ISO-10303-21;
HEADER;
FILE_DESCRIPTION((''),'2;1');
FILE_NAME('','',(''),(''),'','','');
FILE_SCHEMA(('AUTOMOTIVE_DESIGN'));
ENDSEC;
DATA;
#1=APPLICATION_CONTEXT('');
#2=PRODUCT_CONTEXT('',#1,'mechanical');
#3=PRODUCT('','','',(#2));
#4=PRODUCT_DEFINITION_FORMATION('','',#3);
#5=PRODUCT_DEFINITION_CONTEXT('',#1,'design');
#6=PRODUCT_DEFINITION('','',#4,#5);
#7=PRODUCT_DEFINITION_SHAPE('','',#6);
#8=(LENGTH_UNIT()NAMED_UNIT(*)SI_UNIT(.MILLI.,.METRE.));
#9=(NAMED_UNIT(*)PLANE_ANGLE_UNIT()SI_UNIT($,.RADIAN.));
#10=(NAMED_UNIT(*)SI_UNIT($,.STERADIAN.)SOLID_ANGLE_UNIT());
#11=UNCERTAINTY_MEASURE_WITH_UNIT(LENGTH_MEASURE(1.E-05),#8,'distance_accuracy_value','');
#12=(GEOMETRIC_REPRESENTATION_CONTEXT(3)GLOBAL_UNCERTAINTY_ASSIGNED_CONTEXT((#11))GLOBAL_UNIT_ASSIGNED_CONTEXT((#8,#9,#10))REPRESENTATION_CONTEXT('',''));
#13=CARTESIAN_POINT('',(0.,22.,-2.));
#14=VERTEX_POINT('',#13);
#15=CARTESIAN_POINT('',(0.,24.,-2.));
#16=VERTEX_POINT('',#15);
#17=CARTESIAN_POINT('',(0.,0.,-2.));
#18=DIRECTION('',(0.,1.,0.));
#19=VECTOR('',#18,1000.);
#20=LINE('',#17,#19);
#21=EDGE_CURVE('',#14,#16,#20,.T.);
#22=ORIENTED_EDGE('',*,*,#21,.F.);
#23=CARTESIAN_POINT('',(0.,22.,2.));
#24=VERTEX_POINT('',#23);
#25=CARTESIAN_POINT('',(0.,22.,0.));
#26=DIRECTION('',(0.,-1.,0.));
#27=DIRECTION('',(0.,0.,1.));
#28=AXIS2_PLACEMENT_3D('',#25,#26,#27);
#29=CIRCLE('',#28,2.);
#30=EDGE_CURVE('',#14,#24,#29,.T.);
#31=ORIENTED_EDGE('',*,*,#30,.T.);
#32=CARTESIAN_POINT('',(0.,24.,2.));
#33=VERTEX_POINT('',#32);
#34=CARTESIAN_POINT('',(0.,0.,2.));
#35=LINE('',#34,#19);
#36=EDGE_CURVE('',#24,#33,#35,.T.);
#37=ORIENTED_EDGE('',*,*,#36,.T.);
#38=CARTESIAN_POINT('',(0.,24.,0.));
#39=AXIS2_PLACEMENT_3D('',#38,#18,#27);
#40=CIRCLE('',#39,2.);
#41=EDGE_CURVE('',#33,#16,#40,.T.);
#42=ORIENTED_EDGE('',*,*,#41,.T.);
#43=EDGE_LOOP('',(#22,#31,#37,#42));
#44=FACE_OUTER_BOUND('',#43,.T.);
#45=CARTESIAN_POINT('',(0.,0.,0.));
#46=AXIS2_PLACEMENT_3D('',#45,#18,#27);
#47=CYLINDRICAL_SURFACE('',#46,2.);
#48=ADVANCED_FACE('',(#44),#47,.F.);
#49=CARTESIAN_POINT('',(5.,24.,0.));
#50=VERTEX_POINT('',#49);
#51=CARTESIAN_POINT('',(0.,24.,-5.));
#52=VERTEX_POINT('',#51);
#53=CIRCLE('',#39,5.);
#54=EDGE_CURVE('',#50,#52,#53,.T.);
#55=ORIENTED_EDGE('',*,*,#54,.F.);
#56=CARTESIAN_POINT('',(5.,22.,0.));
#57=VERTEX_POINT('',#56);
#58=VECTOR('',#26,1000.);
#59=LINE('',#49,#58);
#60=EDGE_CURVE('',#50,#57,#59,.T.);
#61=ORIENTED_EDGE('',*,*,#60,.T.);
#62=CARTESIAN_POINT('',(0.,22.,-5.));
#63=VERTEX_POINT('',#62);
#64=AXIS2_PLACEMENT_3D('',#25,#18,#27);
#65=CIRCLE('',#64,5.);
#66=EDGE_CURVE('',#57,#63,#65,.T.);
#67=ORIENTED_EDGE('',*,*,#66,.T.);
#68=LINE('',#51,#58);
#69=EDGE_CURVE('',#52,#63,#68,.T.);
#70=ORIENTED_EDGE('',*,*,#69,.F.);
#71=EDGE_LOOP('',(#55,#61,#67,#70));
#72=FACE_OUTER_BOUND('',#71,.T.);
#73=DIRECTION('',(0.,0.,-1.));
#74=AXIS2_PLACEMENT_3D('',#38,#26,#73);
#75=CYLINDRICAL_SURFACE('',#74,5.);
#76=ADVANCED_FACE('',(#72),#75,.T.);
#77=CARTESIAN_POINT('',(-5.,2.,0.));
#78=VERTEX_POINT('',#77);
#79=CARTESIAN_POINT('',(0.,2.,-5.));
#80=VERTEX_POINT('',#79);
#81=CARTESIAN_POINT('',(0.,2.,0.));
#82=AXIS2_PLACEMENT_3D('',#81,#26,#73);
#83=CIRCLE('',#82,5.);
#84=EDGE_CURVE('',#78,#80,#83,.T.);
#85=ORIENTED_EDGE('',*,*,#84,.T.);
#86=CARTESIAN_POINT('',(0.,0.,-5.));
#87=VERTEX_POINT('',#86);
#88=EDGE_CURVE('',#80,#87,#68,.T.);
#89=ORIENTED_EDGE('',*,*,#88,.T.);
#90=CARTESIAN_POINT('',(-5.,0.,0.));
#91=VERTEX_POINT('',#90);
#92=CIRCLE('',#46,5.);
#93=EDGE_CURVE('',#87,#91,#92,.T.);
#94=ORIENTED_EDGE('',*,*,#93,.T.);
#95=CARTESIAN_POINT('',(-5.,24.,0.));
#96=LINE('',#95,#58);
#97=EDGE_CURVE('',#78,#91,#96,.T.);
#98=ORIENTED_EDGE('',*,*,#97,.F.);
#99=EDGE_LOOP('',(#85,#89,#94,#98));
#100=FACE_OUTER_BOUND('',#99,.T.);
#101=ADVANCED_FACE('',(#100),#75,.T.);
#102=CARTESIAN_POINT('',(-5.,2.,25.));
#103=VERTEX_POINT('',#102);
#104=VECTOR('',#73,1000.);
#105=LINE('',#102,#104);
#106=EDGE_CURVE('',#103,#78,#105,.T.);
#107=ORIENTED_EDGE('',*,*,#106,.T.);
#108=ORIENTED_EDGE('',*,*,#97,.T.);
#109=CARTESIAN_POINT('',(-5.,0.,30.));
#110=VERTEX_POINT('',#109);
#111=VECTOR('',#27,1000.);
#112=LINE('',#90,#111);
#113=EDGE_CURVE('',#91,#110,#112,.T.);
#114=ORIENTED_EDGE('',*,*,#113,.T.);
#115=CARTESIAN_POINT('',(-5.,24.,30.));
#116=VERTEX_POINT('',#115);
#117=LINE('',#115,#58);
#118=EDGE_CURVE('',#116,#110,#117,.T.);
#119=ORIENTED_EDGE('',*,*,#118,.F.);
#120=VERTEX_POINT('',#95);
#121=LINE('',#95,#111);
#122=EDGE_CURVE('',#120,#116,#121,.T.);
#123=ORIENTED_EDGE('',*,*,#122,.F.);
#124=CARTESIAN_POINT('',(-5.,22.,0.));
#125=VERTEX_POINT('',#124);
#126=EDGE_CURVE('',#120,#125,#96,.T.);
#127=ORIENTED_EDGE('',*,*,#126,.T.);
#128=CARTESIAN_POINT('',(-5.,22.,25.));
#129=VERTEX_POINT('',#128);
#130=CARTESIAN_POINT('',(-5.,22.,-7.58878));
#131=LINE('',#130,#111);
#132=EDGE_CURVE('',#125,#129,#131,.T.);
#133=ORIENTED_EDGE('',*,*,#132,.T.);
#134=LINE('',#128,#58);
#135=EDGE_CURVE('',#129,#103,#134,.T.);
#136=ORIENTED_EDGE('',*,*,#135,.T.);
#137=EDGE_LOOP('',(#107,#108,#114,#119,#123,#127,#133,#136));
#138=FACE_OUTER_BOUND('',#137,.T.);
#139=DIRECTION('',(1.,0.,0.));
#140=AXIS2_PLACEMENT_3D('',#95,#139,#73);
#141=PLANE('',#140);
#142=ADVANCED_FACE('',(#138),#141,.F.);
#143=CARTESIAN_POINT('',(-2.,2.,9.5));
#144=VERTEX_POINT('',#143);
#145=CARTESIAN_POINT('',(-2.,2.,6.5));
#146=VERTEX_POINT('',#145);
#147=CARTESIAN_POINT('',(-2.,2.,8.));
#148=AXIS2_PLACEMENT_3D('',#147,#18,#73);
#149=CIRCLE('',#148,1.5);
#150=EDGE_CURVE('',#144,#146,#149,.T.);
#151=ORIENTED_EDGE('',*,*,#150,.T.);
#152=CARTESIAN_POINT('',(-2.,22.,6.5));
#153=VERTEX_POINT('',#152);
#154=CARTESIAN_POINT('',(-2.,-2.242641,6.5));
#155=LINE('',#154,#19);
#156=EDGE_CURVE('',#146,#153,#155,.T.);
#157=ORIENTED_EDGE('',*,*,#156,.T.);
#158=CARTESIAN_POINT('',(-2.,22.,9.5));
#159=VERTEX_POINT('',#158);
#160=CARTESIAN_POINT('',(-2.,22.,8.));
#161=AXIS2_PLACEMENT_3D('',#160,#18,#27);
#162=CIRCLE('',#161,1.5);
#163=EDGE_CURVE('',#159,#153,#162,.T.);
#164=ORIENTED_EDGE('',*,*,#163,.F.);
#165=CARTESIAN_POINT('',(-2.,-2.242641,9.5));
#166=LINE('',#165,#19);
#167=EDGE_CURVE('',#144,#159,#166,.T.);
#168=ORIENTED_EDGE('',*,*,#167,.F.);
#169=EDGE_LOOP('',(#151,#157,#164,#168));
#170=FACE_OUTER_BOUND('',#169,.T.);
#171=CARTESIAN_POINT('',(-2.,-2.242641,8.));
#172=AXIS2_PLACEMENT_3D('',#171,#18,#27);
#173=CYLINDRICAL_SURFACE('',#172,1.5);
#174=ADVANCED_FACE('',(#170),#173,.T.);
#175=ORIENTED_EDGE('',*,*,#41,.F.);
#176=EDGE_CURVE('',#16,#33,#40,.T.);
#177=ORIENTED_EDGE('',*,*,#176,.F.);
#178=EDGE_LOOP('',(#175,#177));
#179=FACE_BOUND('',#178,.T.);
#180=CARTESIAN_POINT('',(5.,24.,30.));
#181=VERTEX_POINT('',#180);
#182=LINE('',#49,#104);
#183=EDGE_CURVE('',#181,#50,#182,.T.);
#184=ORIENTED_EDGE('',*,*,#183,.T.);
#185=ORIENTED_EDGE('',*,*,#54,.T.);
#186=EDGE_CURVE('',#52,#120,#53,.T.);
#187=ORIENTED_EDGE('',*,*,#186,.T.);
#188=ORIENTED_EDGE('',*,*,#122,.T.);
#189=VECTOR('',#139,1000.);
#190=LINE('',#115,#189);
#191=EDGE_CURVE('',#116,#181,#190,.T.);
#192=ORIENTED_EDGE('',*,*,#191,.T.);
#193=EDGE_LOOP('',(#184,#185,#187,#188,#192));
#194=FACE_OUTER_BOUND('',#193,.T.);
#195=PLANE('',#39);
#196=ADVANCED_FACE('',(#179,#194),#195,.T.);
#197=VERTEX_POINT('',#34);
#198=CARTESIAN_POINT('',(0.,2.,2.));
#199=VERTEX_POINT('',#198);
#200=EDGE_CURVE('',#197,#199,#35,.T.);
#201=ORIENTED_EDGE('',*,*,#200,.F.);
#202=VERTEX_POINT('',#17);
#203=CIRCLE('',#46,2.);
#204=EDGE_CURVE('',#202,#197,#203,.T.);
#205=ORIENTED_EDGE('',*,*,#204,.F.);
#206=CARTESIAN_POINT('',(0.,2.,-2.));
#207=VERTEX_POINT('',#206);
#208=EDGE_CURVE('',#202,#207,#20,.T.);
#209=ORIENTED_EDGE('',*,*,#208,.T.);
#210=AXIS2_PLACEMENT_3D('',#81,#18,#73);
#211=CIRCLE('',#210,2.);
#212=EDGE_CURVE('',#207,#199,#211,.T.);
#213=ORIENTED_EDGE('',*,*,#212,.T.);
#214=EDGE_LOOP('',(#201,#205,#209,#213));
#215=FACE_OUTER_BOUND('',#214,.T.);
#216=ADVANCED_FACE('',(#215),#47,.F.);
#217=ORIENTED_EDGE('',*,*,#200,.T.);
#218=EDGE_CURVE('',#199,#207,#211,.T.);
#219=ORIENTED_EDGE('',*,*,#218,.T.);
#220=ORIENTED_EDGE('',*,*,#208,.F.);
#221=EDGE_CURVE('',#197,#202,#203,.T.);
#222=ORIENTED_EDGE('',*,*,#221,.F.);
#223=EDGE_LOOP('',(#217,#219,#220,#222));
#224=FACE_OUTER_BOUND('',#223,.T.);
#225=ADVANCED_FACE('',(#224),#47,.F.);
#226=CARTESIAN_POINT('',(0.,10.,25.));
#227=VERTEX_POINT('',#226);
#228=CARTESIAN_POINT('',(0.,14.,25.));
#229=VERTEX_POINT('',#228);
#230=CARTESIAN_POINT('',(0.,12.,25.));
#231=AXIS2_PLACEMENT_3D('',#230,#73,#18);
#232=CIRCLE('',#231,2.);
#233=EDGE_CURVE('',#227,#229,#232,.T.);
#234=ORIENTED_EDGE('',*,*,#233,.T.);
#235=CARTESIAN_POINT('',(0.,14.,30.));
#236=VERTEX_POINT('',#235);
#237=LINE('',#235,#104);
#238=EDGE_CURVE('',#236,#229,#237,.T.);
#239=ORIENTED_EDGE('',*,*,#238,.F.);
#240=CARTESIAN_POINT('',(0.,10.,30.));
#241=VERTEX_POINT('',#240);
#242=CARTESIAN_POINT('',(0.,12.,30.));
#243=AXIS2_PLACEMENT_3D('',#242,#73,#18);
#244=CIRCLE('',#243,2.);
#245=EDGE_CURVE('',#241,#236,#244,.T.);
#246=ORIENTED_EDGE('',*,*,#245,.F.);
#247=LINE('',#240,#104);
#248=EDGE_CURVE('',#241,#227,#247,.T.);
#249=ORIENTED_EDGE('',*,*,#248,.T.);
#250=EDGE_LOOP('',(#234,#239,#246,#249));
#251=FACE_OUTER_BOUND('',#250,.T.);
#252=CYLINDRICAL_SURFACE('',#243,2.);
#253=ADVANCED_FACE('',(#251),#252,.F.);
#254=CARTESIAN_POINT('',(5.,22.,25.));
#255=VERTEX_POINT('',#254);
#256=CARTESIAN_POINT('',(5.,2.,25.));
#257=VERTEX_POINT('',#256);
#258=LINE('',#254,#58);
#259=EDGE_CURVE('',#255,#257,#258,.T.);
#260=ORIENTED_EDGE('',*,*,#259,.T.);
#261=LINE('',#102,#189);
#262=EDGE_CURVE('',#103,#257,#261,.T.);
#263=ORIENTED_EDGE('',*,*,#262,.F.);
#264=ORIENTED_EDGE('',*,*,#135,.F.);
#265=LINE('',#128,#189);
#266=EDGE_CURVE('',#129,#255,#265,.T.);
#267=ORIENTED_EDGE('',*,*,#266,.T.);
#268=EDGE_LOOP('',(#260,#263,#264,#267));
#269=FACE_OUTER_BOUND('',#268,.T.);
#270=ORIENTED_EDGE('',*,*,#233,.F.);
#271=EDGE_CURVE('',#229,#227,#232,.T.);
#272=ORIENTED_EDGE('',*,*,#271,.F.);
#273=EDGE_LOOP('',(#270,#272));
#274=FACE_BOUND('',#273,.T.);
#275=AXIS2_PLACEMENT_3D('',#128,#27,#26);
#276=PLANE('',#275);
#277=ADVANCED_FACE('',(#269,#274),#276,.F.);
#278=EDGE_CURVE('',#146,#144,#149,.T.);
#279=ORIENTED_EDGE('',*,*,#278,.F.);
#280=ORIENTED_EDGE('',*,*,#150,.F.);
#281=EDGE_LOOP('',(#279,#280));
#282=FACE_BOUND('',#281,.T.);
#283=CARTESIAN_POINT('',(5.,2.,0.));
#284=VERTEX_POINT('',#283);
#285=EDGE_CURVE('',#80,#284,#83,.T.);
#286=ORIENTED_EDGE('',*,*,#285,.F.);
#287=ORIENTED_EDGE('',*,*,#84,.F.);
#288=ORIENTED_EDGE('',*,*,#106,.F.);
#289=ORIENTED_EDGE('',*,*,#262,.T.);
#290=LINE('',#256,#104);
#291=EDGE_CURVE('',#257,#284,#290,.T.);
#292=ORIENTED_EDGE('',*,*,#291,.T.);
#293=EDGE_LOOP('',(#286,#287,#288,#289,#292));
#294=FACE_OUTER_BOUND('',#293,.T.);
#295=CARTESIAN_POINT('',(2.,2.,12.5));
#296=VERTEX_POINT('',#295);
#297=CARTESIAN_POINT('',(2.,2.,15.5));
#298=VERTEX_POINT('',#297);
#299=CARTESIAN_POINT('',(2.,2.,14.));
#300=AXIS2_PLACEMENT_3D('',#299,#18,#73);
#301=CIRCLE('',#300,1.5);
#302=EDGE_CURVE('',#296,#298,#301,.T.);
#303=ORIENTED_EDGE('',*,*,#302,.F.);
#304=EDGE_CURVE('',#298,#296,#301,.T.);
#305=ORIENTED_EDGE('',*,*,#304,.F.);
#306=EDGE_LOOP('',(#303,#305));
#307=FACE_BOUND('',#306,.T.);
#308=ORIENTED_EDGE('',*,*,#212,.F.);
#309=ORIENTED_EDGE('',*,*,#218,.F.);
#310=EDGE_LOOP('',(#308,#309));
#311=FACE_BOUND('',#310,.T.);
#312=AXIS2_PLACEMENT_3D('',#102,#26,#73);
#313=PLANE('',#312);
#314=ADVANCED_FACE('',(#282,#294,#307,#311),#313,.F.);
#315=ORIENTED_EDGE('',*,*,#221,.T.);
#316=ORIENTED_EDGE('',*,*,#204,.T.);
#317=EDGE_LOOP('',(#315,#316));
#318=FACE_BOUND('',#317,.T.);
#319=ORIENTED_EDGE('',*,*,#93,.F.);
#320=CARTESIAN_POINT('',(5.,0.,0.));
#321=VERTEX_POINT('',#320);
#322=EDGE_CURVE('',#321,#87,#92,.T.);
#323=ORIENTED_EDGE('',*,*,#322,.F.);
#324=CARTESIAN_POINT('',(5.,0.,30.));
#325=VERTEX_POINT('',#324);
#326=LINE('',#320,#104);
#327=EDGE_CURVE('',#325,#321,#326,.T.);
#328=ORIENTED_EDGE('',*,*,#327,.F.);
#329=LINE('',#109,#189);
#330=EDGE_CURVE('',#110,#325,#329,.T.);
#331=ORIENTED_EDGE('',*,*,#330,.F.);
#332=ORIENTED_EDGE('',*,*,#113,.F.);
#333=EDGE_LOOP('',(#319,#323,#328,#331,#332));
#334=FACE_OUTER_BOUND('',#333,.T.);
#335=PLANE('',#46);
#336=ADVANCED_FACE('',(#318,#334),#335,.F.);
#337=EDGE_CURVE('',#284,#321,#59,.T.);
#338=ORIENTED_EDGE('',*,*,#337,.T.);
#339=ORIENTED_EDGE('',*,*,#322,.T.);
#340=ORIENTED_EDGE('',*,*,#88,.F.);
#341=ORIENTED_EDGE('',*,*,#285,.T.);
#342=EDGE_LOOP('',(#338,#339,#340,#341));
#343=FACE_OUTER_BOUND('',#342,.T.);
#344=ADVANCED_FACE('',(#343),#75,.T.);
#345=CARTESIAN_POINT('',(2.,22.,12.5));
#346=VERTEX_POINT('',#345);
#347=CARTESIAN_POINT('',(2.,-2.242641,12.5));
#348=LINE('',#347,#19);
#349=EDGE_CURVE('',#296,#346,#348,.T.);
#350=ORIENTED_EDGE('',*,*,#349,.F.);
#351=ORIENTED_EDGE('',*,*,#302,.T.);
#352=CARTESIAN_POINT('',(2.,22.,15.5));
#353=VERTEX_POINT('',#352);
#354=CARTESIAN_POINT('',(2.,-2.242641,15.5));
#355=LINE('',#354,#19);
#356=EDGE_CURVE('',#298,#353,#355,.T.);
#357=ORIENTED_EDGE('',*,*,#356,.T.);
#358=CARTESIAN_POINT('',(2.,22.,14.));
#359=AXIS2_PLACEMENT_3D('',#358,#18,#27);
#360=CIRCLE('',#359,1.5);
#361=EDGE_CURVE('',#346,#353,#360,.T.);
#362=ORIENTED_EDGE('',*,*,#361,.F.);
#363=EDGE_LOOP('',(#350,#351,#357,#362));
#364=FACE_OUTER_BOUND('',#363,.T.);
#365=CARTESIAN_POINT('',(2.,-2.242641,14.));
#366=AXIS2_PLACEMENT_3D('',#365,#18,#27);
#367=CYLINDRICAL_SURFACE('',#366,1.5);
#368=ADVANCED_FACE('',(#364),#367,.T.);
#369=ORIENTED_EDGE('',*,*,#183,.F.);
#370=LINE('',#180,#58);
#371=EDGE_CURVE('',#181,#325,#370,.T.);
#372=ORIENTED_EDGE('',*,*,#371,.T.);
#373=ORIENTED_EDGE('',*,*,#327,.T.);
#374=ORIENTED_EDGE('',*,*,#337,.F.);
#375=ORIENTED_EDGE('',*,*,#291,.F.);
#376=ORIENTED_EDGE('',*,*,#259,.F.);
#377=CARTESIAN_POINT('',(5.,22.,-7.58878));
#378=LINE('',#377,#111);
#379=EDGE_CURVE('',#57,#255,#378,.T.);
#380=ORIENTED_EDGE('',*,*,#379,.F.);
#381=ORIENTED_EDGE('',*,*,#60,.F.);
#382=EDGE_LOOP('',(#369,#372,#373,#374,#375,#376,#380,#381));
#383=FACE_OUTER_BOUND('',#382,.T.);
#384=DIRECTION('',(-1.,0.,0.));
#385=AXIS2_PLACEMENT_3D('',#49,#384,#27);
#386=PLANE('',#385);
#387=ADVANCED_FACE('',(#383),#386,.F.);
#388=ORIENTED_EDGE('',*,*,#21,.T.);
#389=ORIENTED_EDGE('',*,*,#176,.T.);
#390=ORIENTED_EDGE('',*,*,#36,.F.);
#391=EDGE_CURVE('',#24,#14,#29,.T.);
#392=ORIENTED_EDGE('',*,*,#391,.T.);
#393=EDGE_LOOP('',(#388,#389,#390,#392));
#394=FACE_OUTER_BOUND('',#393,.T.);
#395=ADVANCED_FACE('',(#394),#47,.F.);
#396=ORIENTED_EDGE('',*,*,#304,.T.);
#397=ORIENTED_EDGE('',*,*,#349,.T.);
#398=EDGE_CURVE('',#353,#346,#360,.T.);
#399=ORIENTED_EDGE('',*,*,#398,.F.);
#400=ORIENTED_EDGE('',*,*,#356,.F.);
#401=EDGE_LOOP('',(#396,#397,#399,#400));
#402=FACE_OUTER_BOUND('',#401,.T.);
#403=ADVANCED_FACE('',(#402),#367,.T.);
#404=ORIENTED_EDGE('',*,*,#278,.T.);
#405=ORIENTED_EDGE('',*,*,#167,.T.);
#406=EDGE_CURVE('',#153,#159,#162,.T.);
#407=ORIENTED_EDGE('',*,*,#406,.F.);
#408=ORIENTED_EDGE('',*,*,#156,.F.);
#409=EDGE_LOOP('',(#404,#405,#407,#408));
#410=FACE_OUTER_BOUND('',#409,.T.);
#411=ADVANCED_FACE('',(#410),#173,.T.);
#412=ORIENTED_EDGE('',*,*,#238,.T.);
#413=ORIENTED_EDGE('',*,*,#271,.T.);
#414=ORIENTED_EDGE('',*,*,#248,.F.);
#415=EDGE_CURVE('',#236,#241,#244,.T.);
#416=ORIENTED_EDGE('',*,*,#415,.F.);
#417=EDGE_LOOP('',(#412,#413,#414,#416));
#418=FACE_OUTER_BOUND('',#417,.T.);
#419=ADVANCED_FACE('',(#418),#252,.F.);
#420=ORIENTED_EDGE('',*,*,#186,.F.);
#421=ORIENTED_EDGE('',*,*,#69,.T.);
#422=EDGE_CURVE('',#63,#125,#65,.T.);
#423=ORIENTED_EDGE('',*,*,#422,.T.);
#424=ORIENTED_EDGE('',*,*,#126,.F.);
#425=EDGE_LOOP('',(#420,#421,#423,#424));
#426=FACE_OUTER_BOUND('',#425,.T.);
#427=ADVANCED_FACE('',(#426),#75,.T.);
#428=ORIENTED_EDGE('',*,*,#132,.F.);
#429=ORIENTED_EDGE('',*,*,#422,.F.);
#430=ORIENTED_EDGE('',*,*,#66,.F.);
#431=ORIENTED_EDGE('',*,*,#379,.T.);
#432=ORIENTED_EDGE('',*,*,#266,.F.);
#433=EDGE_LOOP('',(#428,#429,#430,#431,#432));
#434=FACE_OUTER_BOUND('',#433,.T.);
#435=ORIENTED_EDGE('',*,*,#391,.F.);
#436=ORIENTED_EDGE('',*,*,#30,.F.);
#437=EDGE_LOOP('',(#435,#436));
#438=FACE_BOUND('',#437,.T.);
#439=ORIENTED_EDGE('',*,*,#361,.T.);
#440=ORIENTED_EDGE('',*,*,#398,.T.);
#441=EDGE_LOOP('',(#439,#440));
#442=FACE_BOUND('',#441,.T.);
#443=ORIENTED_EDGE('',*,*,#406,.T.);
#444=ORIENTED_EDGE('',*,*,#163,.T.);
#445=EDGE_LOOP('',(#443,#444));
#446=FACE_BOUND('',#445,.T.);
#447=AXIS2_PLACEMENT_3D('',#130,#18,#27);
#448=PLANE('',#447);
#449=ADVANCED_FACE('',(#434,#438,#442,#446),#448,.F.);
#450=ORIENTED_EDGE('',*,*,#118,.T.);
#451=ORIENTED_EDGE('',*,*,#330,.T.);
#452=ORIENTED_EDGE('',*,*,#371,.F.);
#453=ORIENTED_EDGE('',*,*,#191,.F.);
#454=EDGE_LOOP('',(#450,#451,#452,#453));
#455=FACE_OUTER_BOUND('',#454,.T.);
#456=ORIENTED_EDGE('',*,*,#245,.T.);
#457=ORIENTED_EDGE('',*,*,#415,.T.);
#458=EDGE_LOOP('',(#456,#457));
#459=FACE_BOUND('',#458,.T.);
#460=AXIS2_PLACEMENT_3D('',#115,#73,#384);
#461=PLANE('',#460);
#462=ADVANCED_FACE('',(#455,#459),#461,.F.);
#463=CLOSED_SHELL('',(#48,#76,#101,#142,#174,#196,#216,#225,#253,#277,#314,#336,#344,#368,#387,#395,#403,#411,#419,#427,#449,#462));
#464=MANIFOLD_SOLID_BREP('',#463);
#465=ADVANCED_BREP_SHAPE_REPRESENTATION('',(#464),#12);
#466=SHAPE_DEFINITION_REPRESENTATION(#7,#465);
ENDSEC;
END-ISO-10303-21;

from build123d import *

# Parameters (mm, degrees)
BOSS_EXTRUDE1_DEPTH     = 24
CUT_EXTRUDE2_DEPTH      = 39.742741256
CUT_EXTRUDE2_DEPTH_BACK = 39.742741256
SKETCH4_R               = 2
CUT_EXTRUDE3_DEPTH      = 39.742741256
CUT_EXTRUDE3_DEPTH_BACK = 39.742741256
SKETCH6_W               = 32.588779774
SKETCH6_H               = 20
SKETCH7_R               = 2
CUT_EXTRUDE4_DEPTH      = 39.742741256
SKETCH8_R               = 1.5
BOSS_EXTRUDE3_DEPTH     = 22


with BuildPart() as part:
    # Sketch1 → Boss-Extrude1 (new body)
    with BuildSketch(Plane(origin=(0, 0, 0), x_dir=(1, 0, 0), z_dir=(0, 1, 0))):
        with BuildLine():
            Line((-5, 0), (-5, -30))
            Line((-5, -30), (5, -30))
            Line((5, -30), (5, 0))
            ThreePointArc((5, 0), (0, 5), (-5, 0))
        make_face()
    extrude(amount=BOSS_EXTRUDE1_DEPTH)

    # Sketch4 → Cut-Extrude2 (cut, two sides: drawn at the far end of the back side and taken through both)
    with BuildSketch(Plane(origin=(0, 24, 0), x_dir=(1, 0, 0), z_dir=(0, 1, 0)).offset(-CUT_EXTRUDE2_DEPTH_BACK)):
        with Locations(Location((0, 0, 0), (0, 0, 270))):
            Circle(SKETCH4_R)
    extrude(amount=CUT_EXTRUDE2_DEPTH + CUT_EXTRUDE2_DEPTH_BACK, mode=Mode.SUBTRACT)

    # Sketch6 → Cut-Extrude3 (cut, two sides: drawn at the far end of the back side and taken through both)
    with BuildSketch(Plane(origin=(0, 0, 0), x_dir=(0, 0, -1), z_dir=(1, 0, 0)).offset(-CUT_EXTRUDE3_DEPTH_BACK)):
        with Locations((-8.705610113, 12)):
            Rectangle(SKETCH6_W, SKETCH6_H)
    extrude(amount=CUT_EXTRUDE3_DEPTH + CUT_EXTRUDE3_DEPTH_BACK, mode=Mode.SUBTRACT)

    # Sketch7 → Cut-Extrude4 (cut, through all)
    with BuildSketch(Plane(origin=(0, 0, 25), x_dir=(-1, 0, 0), z_dir=(0, 0, -1))):
        with Locations(Location((0, 12, 0), (0, 0, 90))):
            Circle(SKETCH7_R)
    extrude(amount=-CUT_EXTRUDE4_DEPTH, mode=Mode.SUBTRACT)

    # Sketch8 → Boss-Extrude3 (add)
    with BuildSketch(Plane(origin=(0, 24, 0), x_dir=(1, 0, 0), z_dir=(0, 1, 0))):
        with Locations(Location((-2, -8, 0), (0, 0, 270))):
            Circle(SKETCH8_R)
        with Locations(Location((2, -14, 0), (0, 0, 270))):
            Circle(SKETCH8_R)
    extrude(amount=-BOSS_EXTRUDE3_DEPTH)


solid = part.part
